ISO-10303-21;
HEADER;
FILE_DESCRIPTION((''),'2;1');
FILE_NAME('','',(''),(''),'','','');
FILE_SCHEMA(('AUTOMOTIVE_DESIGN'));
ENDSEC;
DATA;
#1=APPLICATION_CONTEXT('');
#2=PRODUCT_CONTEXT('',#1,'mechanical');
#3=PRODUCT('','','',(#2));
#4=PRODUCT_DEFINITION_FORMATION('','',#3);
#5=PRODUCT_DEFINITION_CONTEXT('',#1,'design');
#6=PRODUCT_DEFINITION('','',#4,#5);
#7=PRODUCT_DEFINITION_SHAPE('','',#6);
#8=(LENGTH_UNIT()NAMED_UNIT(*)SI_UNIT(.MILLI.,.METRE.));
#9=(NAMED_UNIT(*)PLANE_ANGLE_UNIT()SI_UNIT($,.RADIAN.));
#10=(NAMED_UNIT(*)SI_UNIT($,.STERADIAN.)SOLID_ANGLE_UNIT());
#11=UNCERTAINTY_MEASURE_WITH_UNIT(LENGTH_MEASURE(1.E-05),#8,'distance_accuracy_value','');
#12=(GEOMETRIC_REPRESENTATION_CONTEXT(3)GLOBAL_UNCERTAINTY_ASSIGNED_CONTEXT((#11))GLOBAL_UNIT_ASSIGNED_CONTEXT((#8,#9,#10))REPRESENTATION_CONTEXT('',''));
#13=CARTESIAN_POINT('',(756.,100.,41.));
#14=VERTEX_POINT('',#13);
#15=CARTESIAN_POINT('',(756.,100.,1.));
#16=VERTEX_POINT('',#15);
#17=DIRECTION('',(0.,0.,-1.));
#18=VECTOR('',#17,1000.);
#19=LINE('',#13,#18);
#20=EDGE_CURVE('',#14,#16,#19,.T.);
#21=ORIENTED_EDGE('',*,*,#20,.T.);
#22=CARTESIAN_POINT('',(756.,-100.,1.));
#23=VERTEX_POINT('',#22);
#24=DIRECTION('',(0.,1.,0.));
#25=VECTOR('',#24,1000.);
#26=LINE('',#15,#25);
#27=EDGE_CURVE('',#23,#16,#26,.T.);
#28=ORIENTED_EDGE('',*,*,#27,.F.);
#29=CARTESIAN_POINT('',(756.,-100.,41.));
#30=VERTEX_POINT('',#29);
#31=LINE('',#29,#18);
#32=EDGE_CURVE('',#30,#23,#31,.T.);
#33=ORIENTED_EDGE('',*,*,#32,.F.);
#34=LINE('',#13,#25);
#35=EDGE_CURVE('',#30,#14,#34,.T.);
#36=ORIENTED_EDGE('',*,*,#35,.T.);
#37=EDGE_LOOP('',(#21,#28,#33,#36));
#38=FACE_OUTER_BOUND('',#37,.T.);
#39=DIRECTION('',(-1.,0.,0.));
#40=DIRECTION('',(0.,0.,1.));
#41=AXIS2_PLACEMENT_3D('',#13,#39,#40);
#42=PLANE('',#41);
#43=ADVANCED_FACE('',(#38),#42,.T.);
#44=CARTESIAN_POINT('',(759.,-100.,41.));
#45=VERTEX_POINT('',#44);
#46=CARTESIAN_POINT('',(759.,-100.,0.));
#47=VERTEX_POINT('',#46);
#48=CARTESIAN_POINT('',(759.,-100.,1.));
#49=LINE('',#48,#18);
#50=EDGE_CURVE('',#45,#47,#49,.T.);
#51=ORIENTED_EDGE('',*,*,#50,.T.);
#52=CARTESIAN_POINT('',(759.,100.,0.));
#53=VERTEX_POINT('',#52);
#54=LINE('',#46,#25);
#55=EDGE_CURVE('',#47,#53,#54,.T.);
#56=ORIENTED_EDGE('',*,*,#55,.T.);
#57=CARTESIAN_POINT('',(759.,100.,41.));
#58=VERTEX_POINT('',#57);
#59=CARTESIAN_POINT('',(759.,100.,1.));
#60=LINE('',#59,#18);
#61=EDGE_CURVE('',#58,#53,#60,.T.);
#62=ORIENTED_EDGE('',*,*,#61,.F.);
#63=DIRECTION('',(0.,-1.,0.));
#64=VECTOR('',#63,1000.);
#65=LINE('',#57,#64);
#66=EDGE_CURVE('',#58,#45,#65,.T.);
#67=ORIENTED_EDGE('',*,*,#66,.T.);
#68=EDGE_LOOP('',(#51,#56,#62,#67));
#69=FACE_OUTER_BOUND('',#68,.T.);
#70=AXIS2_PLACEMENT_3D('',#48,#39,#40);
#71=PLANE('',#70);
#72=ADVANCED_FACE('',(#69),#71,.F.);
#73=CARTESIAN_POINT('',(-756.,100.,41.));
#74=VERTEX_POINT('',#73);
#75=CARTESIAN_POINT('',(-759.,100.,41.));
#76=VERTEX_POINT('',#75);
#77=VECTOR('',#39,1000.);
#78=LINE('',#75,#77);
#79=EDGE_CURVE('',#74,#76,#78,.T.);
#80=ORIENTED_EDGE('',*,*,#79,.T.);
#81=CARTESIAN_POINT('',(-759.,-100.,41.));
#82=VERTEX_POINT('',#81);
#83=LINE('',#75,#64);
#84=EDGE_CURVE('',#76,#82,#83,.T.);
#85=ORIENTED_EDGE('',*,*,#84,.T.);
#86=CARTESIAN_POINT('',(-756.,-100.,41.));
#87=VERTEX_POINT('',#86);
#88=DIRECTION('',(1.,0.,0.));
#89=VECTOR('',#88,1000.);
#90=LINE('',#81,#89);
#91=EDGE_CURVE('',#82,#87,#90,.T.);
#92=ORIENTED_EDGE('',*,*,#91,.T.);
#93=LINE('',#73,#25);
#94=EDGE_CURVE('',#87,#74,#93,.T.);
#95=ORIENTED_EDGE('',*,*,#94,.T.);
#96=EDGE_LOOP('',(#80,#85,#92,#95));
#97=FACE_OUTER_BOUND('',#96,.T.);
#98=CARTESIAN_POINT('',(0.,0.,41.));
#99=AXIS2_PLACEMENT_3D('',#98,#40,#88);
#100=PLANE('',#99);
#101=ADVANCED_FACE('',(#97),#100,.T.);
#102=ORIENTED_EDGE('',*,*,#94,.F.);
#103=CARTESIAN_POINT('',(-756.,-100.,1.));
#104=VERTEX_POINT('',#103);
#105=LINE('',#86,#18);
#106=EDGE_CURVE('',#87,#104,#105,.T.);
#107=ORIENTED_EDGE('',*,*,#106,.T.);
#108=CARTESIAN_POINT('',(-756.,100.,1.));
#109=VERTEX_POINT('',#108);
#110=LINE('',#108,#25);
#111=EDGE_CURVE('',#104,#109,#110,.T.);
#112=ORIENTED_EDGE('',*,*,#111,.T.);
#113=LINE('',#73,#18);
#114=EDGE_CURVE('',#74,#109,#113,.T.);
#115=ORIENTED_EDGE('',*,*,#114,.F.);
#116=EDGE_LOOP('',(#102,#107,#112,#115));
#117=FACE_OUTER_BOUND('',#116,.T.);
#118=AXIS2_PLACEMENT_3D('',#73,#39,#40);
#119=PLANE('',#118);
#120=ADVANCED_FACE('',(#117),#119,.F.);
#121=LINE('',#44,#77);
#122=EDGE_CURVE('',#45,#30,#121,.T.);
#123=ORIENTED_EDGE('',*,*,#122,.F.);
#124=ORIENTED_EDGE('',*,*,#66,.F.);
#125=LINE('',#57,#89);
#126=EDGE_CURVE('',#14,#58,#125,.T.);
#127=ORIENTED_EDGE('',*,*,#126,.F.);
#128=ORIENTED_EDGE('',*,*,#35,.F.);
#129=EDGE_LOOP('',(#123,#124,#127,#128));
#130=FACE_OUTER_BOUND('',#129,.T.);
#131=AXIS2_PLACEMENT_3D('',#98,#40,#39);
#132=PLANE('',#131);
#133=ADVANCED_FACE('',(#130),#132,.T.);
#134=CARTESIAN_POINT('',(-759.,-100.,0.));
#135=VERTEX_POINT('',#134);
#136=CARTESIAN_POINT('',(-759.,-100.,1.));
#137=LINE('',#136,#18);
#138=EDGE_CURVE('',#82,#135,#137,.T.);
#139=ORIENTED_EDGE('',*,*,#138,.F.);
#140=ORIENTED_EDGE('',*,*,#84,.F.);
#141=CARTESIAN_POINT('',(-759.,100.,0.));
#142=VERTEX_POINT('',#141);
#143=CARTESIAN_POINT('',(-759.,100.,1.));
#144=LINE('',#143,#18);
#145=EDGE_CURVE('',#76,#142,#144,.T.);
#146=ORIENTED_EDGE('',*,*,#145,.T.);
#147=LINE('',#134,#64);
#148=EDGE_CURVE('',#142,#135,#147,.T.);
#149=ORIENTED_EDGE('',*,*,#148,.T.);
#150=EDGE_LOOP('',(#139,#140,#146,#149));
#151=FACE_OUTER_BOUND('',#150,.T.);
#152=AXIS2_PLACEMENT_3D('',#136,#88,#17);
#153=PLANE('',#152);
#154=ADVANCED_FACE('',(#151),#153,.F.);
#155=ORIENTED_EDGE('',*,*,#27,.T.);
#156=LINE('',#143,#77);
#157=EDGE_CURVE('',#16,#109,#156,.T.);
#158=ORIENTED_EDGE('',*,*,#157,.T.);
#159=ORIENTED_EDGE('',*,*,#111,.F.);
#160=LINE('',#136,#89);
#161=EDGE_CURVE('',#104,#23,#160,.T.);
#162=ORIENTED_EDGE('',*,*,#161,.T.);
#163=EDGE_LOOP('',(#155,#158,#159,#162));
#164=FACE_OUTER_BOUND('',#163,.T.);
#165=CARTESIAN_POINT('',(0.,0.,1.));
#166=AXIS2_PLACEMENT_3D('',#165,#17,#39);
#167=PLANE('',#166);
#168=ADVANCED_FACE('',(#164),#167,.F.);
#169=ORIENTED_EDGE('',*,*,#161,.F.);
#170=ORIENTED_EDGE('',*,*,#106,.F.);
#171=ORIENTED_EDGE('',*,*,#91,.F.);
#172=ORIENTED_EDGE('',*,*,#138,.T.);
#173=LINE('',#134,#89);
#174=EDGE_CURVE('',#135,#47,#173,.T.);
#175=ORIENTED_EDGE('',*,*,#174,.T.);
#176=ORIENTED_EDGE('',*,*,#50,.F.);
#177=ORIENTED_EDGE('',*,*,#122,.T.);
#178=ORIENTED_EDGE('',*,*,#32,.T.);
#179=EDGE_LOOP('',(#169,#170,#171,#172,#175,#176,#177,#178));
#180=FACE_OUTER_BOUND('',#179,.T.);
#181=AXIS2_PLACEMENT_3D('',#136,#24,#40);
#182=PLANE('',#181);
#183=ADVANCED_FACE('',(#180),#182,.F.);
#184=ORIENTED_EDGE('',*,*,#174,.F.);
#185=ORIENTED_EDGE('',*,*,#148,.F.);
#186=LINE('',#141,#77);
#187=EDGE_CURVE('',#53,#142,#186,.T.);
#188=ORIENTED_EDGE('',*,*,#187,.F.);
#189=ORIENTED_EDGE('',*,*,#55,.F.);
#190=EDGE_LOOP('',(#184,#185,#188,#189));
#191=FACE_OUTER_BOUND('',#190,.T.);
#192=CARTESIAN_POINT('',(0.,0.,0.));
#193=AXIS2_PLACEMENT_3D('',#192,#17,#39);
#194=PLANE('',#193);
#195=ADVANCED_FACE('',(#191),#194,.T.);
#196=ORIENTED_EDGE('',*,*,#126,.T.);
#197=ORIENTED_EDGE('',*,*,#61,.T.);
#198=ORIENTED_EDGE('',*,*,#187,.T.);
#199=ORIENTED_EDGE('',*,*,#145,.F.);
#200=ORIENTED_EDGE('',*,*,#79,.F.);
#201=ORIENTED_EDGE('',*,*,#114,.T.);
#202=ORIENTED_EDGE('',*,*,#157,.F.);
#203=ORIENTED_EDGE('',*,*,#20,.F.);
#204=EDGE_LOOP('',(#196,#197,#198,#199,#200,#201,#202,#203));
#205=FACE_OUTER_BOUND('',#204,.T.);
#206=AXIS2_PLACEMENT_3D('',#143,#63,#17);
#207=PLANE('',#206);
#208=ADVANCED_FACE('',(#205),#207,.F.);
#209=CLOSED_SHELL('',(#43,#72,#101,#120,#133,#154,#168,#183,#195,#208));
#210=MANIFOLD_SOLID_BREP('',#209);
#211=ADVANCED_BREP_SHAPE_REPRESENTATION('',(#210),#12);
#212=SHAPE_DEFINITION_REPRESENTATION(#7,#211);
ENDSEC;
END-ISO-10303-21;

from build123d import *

# Parameters (mm, degrees)
SKETCH_1_W      = 1518
SKETCH_1_H      = 200
EXTRUDE_1_DEPTH = 1
SKETCH_2_W      = 3
SKETCH_2_H      = 200
EXTRUDE_2_DEPTH = 40


with BuildPart() as part:
    # 草图1 → 凸台-拉伸1 (new body)
    with BuildSketch(Plane.XY):
        Rectangle(SKETCH_1_W, SKETCH_1_H)
    extrude(amount=EXTRUDE_1_DEPTH)

    # 草图2 → 凸台-拉伸2 (add)
    with BuildSketch(Plane.XY.offset(1)):
        with Locations((-757.5, 0)):
            Rectangle(SKETCH_2_W, SKETCH_2_H)
    extrude_2 = extrude(amount=EXTRUDE_2_DEPTH)

    # 镜向1: 凸台-拉伸2 across plane
    add(extrude_2.mirror(Plane(origin=(0, 0, 0), x_dir=(0, 0, 1), z_dir=(1, 0, 0))))


solid = part.part
